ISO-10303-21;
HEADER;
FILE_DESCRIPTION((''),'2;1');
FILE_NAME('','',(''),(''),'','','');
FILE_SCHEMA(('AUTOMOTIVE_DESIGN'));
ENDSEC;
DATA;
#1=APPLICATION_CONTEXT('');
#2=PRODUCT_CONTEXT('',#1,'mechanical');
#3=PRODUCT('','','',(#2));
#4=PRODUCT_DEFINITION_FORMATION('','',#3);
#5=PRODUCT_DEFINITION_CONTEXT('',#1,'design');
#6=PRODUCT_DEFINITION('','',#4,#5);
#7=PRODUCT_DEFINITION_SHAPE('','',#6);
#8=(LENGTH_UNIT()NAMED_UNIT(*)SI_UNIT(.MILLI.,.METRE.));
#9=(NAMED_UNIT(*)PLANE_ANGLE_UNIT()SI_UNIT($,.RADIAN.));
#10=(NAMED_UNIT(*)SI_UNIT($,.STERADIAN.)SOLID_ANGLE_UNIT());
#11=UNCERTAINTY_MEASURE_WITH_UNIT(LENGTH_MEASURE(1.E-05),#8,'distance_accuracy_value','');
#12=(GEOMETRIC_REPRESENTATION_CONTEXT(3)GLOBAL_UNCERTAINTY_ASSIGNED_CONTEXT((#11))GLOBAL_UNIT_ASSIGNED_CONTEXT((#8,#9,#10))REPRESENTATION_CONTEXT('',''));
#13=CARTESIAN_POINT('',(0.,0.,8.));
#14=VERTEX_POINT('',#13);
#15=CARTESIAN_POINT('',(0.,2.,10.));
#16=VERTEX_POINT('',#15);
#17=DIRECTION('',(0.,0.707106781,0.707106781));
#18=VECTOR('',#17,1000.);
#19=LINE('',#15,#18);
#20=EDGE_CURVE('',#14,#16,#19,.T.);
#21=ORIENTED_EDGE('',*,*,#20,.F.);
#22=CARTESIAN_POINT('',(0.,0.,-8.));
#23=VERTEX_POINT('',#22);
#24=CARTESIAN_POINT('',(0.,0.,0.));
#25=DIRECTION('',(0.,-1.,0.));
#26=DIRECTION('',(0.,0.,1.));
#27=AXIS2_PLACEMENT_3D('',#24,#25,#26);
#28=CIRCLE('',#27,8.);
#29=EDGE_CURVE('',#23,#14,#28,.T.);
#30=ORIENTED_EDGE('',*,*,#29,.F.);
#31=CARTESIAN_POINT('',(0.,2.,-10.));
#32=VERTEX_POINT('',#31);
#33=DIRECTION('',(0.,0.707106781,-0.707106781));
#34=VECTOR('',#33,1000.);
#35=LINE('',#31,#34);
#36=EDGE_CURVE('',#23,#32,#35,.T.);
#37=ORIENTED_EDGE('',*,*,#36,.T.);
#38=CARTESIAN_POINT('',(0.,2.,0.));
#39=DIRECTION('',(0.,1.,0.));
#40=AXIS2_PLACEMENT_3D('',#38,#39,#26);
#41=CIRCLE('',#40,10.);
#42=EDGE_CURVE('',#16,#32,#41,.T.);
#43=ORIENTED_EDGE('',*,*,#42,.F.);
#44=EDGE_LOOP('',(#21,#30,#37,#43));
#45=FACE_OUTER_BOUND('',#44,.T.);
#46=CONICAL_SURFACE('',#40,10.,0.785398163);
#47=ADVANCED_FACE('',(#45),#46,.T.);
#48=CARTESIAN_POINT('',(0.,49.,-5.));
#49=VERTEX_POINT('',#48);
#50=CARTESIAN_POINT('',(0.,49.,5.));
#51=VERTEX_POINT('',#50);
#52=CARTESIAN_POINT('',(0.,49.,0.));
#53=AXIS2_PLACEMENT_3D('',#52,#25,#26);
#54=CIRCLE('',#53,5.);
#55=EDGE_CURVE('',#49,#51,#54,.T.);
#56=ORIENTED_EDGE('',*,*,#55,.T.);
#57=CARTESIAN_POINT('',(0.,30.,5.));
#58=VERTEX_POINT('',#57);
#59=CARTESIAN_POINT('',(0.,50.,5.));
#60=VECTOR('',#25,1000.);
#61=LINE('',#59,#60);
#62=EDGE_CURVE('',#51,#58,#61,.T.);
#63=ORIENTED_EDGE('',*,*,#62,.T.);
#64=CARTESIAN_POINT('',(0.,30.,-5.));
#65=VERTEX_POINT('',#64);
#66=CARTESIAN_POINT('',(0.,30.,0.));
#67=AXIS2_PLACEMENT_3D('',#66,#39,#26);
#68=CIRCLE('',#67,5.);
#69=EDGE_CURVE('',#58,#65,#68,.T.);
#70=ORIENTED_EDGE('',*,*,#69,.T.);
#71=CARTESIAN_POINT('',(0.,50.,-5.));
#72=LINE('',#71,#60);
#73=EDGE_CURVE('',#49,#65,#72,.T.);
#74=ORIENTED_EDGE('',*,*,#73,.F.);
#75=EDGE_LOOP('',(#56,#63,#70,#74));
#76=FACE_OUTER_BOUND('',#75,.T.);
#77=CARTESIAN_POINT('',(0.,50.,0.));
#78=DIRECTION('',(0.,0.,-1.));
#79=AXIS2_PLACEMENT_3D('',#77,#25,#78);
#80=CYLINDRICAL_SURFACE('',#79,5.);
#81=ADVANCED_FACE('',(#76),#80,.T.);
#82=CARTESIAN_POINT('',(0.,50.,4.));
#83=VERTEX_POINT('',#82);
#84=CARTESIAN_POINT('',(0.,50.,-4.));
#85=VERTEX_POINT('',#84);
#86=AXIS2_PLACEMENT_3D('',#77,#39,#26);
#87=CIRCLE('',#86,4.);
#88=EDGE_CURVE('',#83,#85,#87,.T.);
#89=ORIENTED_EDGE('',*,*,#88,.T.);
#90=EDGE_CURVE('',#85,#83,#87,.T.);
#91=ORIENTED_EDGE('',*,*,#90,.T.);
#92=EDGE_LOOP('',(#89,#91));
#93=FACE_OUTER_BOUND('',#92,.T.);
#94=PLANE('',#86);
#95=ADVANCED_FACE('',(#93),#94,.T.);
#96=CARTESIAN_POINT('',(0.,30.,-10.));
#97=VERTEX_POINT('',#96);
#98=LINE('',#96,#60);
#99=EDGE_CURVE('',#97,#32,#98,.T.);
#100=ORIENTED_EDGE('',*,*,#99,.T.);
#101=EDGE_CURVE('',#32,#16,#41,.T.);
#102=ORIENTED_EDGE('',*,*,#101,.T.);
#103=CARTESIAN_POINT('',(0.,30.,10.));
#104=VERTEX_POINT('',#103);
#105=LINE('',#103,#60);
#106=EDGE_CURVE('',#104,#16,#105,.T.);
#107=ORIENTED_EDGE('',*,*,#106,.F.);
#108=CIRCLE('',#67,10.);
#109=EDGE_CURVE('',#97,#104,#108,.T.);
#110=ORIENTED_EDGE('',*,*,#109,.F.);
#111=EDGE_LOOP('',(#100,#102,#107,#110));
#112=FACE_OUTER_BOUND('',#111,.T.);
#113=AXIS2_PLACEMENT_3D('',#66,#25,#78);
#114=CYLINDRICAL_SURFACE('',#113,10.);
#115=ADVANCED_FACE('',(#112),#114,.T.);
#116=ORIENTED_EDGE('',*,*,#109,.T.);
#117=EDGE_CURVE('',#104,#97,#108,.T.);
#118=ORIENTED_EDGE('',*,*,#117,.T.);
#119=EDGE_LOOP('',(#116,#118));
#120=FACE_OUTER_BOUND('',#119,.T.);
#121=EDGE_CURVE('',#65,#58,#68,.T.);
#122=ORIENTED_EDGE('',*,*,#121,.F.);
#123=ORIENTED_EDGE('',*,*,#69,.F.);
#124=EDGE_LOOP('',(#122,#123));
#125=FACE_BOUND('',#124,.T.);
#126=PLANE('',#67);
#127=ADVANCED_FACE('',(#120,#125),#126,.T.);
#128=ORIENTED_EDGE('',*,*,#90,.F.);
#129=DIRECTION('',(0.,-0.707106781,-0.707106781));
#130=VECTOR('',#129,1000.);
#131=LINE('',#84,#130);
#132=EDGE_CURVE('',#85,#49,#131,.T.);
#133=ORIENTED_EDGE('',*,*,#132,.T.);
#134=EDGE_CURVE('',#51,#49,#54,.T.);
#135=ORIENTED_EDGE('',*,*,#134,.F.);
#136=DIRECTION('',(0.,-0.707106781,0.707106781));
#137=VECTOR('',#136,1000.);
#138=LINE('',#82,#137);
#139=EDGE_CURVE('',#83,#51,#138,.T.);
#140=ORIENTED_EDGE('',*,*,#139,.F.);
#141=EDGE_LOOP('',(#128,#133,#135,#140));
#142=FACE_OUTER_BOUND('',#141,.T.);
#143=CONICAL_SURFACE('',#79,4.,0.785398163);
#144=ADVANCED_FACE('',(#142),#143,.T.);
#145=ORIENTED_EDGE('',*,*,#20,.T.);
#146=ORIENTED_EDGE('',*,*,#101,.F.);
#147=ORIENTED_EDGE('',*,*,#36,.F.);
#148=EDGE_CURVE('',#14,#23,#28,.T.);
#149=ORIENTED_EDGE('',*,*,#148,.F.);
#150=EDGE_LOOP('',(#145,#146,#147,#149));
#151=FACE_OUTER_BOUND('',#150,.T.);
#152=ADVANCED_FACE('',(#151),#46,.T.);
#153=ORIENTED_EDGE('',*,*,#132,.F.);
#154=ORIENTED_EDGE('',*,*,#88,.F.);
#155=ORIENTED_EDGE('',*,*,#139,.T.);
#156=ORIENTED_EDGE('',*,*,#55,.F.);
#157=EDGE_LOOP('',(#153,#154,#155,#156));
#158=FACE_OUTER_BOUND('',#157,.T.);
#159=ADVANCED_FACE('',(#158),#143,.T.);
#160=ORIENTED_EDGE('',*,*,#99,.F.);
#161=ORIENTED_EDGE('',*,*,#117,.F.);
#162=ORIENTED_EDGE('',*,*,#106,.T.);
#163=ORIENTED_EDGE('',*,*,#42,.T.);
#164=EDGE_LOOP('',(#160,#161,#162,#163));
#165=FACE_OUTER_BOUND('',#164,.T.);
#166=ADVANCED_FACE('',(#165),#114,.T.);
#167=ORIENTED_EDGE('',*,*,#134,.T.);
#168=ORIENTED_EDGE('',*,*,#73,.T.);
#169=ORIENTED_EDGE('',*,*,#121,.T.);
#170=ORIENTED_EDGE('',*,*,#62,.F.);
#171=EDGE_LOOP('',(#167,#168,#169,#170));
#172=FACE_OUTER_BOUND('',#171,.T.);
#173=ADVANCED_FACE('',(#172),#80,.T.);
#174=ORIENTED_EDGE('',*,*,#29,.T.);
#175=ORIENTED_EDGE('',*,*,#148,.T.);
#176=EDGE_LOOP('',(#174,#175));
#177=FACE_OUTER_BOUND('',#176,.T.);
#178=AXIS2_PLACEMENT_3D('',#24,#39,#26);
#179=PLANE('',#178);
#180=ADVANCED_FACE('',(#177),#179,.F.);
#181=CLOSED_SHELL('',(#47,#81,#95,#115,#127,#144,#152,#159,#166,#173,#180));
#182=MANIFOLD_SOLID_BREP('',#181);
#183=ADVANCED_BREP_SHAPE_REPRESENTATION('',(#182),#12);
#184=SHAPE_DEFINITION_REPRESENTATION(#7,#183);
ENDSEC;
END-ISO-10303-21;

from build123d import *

# Parameters (mm, degrees)
SKETCH1_R           = 10
BOSS_EXTRUDE1_DEPTH = 30
SKETCH2_R           = 5
BOSS_EXTRUDE2_DEPTH = 20
CHAMFER1_SIZE       = 2
CHAMFER2_SIZE       = 1


with BuildPart() as part:
    # Sketch1 → Boss-Extrude1 (new body)
    with BuildSketch(Plane(origin=(0, 0, 0), x_dir=(1, 0, 0), z_dir=(0, 1, 0))):
        with Locations(Location((0, 0, 0), (0, 0, 270))):
            Circle(SKETCH1_R)
    extrude(amount=BOSS_EXTRUDE1_DEPTH)

    # Sketch2 → Boss-Extrude2 (add)
    with BuildSketch(Plane(origin=(0, 30, 0), x_dir=(1, 0, 0), z_dir=(0, 1, 0))):
        with Locations(Location((0, 0, 0), (0, 0, 270))):
            Circle(SKETCH2_R)
    extrude(amount=BOSS_EXTRUDE2_DEPTH)

    # Chamfer1
    chamfer1_edges = [part.edges().sort_by_distance(p)[0] for p in [
        (0, 0, -10),
    ]]
    chamfer(chamfer1_edges, length=CHAMFER1_SIZE)

    # Chamfer2
    chamfer2_edges = [part.edges().sort_by_distance(p)[0] for p in [
        (0, 50, -5),
    ]]
    chamfer(chamfer2_edges, length=CHAMFER2_SIZE)


solid = part.part
